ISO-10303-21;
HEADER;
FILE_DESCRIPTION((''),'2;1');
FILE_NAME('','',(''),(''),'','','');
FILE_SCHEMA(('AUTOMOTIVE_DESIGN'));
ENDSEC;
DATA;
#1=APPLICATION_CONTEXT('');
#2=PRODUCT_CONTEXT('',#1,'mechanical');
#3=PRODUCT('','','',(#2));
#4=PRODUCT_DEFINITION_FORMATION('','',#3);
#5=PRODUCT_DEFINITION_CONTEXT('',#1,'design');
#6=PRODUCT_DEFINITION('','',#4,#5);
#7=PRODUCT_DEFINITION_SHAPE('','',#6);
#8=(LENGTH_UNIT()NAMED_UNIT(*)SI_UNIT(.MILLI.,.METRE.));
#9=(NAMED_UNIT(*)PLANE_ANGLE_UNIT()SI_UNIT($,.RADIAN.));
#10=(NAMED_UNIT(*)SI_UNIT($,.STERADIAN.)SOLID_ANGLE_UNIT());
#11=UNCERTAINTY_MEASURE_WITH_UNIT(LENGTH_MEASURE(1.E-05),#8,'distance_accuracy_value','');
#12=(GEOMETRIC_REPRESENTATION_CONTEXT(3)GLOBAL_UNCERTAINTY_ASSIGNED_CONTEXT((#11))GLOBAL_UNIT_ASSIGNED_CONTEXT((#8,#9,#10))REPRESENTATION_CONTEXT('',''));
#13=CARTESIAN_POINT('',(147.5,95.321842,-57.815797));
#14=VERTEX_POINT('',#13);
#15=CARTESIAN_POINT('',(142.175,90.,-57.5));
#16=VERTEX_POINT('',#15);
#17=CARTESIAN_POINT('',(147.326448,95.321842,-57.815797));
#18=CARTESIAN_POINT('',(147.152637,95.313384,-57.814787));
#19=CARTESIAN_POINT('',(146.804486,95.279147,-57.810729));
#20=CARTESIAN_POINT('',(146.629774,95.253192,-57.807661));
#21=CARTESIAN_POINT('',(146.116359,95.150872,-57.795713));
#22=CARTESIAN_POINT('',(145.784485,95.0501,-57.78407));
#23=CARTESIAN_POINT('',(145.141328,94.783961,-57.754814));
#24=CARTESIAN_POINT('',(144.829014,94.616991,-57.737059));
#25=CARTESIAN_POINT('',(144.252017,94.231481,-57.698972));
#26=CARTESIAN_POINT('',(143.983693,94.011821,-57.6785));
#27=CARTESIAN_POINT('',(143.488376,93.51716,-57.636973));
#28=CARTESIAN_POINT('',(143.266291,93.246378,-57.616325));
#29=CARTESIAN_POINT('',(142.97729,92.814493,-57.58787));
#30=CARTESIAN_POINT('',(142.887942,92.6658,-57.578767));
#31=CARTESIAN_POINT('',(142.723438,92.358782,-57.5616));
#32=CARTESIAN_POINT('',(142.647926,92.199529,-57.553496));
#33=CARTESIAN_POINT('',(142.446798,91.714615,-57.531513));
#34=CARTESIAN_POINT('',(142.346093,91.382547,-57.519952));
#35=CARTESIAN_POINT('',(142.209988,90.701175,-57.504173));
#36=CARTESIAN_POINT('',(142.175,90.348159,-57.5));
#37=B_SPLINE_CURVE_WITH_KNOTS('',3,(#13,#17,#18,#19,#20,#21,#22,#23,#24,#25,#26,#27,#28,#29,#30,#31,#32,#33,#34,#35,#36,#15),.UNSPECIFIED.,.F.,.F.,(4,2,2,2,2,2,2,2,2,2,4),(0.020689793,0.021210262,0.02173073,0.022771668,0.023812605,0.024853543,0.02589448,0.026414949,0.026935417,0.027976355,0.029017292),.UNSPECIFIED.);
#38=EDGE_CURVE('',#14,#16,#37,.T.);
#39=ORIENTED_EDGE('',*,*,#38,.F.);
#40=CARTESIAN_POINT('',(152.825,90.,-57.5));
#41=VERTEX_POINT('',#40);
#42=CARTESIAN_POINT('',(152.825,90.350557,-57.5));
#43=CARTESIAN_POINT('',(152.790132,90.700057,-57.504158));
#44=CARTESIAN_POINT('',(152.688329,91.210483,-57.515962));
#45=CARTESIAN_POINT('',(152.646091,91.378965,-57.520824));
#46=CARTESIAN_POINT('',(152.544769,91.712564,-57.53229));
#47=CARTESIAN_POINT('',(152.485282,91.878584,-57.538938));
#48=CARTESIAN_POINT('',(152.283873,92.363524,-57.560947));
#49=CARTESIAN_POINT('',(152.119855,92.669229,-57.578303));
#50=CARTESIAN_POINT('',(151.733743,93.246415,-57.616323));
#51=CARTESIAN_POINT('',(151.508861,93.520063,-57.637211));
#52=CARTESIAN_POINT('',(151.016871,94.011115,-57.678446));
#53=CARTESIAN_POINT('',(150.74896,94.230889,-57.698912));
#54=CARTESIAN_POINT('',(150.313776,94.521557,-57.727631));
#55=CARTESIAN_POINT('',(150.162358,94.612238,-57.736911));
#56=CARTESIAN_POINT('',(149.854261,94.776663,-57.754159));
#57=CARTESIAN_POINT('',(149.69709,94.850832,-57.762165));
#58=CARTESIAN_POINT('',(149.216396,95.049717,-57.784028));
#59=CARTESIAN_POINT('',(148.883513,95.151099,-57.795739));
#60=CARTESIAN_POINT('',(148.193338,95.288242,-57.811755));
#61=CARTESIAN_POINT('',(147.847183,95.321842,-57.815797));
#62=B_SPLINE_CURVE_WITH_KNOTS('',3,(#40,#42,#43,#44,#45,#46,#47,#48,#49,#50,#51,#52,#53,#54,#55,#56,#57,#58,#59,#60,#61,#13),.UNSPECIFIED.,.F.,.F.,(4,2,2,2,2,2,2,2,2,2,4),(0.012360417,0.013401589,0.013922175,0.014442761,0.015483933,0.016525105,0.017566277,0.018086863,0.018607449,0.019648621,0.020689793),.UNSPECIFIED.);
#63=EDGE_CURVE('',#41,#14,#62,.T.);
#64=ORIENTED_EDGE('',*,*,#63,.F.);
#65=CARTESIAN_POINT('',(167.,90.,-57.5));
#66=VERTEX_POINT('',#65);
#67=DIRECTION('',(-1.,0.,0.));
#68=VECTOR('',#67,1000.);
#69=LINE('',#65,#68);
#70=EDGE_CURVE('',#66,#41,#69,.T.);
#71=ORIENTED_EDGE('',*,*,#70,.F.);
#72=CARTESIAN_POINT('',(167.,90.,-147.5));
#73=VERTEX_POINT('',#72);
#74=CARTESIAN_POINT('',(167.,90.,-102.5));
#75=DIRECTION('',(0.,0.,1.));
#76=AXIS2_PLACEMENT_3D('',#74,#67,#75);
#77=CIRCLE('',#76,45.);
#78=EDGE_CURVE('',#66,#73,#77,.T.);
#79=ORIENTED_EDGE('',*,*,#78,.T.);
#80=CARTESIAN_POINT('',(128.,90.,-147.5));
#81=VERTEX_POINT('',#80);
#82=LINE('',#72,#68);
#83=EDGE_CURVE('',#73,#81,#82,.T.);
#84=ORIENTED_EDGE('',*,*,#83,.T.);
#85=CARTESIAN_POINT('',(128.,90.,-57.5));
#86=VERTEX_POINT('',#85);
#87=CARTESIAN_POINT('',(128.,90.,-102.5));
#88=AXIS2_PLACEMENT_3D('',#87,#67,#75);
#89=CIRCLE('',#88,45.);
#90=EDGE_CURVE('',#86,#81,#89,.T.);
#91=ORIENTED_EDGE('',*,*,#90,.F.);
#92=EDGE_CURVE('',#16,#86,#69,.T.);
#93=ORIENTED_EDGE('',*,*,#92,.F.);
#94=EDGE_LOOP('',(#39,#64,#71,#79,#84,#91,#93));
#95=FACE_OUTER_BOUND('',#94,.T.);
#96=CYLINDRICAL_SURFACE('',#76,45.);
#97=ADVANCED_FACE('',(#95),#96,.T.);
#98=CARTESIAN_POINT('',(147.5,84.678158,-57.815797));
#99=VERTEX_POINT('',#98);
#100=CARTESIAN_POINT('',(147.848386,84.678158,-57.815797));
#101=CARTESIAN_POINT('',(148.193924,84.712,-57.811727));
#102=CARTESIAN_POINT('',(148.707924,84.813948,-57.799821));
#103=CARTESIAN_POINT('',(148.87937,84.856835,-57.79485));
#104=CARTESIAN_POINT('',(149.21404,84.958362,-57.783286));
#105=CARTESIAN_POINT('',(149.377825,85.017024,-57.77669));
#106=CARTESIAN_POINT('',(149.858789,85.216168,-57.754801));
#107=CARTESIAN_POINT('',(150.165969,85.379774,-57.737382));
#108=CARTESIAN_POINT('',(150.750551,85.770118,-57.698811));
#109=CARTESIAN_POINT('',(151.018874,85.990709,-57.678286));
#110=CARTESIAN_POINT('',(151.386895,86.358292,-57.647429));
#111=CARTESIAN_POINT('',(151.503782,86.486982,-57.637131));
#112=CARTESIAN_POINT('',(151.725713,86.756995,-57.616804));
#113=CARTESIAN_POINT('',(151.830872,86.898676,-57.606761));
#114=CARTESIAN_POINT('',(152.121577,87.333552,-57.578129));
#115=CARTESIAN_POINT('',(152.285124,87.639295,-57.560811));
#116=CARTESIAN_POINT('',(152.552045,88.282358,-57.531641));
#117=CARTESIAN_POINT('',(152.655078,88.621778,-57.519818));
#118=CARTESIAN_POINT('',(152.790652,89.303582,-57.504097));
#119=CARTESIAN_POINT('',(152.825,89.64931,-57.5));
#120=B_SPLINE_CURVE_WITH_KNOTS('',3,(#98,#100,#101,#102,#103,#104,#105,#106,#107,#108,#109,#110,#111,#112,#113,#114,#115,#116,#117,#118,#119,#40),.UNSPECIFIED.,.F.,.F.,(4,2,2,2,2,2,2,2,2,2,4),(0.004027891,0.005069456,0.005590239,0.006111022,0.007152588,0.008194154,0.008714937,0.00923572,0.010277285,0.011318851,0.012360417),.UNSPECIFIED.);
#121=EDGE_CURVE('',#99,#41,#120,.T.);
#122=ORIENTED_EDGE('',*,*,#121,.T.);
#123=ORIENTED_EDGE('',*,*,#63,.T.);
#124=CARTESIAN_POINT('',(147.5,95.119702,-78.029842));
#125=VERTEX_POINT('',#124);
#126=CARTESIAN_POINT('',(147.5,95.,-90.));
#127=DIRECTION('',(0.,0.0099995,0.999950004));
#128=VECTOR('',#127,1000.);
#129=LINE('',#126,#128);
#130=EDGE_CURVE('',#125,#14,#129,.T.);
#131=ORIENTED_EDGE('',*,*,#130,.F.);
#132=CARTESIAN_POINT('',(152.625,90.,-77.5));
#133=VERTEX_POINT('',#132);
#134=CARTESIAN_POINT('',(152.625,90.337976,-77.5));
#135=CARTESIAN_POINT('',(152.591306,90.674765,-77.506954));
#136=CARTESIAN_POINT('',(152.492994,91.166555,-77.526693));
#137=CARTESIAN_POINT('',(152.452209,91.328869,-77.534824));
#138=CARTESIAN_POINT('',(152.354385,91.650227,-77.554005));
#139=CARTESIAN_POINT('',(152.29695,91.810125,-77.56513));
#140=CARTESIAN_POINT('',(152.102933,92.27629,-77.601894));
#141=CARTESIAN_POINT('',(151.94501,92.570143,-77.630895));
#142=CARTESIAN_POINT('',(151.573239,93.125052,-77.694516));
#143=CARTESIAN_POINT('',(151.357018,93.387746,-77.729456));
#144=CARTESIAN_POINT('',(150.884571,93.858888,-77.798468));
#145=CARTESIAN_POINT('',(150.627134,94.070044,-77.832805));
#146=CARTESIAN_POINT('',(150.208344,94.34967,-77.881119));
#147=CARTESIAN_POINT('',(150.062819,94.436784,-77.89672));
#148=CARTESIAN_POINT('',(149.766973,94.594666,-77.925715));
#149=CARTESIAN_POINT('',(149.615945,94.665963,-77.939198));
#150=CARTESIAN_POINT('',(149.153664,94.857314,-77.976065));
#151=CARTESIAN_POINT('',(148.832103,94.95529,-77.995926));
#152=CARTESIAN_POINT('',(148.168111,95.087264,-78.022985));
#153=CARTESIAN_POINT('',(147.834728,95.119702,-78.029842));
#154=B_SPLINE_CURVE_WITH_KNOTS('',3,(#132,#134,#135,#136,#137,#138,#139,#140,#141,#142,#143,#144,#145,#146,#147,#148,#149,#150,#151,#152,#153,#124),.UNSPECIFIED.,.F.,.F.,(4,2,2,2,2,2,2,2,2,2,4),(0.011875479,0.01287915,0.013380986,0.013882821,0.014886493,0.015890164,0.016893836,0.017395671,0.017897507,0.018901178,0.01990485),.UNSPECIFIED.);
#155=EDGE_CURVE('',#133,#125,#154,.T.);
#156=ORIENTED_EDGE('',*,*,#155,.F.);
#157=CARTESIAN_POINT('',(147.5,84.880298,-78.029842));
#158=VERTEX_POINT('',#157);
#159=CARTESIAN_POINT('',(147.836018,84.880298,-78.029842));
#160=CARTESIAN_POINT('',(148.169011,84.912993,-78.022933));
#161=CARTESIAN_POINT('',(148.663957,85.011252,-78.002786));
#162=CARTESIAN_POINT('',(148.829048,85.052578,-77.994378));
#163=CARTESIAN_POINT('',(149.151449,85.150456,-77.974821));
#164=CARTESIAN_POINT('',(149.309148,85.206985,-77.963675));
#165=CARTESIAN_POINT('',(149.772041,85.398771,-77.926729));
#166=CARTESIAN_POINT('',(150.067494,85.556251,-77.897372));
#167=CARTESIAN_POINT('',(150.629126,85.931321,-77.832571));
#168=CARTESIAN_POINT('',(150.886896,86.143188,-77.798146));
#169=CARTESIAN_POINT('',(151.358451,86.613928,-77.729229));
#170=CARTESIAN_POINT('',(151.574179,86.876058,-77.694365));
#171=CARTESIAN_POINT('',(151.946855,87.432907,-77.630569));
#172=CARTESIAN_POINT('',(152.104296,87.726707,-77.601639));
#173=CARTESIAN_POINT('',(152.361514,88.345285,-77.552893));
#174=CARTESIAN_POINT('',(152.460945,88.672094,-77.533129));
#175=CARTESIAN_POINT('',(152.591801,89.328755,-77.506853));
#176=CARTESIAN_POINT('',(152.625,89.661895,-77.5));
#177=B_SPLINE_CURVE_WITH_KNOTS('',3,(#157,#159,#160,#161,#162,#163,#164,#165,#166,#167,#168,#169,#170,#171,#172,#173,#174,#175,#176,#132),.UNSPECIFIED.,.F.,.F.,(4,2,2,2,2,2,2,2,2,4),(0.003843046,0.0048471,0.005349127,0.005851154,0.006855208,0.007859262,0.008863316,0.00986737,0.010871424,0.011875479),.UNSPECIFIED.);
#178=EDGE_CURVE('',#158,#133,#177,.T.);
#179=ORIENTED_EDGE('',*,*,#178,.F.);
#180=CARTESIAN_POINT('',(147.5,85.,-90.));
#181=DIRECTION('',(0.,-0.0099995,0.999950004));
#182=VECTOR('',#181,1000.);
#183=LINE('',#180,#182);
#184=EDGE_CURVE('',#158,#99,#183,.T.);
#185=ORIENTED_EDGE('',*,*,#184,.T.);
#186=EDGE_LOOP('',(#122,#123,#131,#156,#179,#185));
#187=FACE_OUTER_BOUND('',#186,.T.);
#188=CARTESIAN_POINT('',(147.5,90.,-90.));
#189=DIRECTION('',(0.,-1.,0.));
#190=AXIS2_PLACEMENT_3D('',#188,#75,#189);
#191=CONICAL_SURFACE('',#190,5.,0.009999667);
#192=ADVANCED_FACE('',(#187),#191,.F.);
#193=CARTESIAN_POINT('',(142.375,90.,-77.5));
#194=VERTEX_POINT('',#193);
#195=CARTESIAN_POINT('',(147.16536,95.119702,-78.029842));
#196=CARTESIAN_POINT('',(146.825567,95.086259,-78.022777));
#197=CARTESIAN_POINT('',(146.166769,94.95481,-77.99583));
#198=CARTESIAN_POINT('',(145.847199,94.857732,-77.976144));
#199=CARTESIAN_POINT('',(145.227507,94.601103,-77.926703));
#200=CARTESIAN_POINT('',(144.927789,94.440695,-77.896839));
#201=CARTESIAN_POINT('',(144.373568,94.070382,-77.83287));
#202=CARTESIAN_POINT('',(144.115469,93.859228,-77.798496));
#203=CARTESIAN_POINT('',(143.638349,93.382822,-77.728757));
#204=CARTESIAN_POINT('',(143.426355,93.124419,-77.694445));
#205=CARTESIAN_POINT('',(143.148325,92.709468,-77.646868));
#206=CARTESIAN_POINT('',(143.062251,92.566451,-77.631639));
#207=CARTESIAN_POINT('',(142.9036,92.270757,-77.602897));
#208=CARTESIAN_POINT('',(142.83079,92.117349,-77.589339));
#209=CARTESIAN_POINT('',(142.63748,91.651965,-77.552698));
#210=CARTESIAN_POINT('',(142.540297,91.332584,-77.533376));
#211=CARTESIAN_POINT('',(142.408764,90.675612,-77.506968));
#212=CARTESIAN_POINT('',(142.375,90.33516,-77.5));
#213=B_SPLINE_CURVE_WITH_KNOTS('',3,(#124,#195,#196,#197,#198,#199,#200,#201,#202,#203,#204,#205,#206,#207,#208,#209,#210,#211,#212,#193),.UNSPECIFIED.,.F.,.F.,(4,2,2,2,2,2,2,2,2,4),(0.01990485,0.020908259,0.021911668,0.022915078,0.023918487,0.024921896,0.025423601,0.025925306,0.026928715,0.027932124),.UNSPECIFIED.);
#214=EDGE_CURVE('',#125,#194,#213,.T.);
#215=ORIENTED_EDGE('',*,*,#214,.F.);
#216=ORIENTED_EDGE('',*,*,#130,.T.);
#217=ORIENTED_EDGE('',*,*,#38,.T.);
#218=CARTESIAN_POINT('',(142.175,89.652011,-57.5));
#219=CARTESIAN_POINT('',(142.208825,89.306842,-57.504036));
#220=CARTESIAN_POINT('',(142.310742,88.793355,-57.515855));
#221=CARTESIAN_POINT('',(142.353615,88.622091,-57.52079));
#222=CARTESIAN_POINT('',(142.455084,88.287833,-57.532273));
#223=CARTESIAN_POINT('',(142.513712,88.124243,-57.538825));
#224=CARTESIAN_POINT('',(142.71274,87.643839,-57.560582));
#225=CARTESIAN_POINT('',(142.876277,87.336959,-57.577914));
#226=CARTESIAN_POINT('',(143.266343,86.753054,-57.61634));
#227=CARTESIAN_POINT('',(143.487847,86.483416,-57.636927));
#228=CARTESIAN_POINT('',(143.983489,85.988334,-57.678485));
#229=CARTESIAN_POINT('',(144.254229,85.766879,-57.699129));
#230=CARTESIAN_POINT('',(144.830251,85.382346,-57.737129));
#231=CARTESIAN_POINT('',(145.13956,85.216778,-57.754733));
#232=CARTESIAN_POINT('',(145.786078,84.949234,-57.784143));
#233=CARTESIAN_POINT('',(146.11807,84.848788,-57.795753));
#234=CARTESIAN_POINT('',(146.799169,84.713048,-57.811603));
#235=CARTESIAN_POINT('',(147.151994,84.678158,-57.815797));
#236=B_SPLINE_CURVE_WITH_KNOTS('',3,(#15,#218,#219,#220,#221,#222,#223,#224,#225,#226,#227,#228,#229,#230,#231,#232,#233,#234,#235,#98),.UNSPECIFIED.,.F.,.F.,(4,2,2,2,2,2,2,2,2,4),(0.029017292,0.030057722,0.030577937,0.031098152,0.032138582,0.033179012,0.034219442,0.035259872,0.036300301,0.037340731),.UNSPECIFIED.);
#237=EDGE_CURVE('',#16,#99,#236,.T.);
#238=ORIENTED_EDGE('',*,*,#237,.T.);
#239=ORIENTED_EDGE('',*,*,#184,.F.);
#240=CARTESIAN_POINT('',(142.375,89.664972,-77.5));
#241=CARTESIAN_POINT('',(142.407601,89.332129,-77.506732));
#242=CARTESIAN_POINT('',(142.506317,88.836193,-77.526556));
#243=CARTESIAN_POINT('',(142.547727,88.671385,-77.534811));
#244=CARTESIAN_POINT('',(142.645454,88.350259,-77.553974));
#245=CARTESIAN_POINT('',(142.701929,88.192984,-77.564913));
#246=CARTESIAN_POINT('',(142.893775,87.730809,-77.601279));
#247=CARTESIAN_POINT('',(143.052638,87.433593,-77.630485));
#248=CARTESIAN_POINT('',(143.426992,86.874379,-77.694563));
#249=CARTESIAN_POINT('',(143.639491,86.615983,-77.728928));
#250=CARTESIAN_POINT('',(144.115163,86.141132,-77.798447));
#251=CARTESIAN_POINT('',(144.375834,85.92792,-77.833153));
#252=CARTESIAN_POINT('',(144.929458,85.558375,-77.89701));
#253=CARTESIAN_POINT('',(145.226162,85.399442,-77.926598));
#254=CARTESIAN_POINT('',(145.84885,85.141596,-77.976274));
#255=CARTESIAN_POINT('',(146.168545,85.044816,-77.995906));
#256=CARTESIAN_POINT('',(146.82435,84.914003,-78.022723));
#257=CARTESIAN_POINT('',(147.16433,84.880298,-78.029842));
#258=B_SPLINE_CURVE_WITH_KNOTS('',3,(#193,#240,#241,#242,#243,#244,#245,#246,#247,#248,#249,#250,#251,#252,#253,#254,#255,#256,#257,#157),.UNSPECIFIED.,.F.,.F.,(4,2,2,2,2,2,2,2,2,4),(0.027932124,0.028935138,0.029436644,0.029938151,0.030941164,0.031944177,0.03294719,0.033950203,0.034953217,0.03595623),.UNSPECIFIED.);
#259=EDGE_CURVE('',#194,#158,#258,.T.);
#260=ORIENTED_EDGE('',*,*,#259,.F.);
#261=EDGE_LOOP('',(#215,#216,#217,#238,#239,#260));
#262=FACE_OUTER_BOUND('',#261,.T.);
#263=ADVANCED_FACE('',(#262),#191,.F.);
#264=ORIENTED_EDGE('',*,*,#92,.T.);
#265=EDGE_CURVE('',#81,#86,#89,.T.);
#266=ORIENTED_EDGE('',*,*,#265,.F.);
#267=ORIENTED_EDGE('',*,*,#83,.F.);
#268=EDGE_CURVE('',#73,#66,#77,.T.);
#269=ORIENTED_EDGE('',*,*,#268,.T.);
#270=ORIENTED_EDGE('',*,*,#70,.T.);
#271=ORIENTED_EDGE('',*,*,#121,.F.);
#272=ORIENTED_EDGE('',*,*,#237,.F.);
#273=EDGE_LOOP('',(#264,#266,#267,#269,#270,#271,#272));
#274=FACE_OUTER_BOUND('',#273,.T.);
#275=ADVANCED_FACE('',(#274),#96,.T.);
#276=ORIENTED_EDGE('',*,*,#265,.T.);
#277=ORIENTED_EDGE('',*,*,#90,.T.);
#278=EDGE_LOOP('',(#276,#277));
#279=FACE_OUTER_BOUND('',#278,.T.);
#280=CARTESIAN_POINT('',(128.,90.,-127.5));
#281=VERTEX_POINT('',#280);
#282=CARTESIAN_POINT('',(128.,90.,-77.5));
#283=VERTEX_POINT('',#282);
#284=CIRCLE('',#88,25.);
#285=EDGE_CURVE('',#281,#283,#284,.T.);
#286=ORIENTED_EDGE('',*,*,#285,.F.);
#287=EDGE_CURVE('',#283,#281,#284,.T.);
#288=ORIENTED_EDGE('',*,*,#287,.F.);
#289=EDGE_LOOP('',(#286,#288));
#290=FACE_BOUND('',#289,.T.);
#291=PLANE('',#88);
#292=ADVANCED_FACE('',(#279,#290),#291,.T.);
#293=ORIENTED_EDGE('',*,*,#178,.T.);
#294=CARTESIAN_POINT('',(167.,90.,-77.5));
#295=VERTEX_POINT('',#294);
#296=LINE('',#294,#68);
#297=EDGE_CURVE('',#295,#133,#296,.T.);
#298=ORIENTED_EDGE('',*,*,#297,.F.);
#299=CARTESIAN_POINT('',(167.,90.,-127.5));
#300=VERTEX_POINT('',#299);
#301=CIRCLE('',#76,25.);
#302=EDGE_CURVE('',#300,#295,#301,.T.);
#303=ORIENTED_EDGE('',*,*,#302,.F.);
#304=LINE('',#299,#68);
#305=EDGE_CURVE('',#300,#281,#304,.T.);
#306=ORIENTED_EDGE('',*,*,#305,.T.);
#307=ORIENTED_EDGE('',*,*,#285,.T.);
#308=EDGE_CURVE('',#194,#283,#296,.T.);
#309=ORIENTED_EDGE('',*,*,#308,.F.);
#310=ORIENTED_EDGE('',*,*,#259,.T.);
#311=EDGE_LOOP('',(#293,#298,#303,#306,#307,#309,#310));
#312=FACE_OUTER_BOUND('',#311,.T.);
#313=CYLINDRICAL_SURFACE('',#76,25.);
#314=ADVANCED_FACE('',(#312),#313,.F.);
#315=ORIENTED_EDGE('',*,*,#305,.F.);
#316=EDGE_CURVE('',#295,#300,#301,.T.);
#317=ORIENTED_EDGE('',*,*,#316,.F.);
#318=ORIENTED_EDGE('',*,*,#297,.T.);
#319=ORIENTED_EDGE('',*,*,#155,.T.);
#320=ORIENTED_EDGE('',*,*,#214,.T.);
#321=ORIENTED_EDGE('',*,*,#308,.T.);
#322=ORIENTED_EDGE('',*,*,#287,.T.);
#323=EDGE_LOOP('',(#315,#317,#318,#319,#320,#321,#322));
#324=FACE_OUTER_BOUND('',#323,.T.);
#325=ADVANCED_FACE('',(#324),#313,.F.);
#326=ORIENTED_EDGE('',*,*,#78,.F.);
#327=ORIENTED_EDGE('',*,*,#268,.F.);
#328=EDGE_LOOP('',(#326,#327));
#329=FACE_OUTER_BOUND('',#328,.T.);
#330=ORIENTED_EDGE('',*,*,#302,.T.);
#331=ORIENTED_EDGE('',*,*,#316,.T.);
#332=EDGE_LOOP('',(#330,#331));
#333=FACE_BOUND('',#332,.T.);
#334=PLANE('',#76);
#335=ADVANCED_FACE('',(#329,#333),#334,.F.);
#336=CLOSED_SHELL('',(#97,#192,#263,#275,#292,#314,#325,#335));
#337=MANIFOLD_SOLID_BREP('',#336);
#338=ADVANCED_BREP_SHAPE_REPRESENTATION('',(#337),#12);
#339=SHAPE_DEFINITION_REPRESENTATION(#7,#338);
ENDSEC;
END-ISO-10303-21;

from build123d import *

# Parameters (mm, degrees)
SKETCH1_R           = 45
SKETCH1_R_2         = 25
BOSS_EXTRUDE1_DEPTH = 39


with BuildPart() as part:
    # Sketch1 → Boss-Extrude1 (new body)
    with BuildSketch(Plane.ZY.offset(-128)):
        with Locations((-102.5, 90)):
            Circle(SKETCH1_R)
        with Locations((-102.5, 90)):
            Circle(SKETCH1_R_2, mode=Mode.SUBTRACT)
    extrude(amount=-BOSS_EXTRUDE1_DEPTH)

    # Sketch2 → Cut-Revolve1 (revolve, cut)
    with BuildSketch(Plane(origin=(147.5, 0, 0), x_dir=(0, 0, -1), z_dir=(1, 0, 0)), mode=Mode.PRIVATE) as cut_revolve1_sk:
        Polygon((0, 90), (0, 95.9), (90, 95), (90, 90), align=None)
    revolve(cut_revolve1_sk.sketch.rotate(Axis((147.5, 90, -102.5), (0, 0, 1)), 269.999999962), axis=Axis((147.5, 90, -102.5), (0, 0, 1)), mode=Mode.SUBTRACT)


solid = part.part
